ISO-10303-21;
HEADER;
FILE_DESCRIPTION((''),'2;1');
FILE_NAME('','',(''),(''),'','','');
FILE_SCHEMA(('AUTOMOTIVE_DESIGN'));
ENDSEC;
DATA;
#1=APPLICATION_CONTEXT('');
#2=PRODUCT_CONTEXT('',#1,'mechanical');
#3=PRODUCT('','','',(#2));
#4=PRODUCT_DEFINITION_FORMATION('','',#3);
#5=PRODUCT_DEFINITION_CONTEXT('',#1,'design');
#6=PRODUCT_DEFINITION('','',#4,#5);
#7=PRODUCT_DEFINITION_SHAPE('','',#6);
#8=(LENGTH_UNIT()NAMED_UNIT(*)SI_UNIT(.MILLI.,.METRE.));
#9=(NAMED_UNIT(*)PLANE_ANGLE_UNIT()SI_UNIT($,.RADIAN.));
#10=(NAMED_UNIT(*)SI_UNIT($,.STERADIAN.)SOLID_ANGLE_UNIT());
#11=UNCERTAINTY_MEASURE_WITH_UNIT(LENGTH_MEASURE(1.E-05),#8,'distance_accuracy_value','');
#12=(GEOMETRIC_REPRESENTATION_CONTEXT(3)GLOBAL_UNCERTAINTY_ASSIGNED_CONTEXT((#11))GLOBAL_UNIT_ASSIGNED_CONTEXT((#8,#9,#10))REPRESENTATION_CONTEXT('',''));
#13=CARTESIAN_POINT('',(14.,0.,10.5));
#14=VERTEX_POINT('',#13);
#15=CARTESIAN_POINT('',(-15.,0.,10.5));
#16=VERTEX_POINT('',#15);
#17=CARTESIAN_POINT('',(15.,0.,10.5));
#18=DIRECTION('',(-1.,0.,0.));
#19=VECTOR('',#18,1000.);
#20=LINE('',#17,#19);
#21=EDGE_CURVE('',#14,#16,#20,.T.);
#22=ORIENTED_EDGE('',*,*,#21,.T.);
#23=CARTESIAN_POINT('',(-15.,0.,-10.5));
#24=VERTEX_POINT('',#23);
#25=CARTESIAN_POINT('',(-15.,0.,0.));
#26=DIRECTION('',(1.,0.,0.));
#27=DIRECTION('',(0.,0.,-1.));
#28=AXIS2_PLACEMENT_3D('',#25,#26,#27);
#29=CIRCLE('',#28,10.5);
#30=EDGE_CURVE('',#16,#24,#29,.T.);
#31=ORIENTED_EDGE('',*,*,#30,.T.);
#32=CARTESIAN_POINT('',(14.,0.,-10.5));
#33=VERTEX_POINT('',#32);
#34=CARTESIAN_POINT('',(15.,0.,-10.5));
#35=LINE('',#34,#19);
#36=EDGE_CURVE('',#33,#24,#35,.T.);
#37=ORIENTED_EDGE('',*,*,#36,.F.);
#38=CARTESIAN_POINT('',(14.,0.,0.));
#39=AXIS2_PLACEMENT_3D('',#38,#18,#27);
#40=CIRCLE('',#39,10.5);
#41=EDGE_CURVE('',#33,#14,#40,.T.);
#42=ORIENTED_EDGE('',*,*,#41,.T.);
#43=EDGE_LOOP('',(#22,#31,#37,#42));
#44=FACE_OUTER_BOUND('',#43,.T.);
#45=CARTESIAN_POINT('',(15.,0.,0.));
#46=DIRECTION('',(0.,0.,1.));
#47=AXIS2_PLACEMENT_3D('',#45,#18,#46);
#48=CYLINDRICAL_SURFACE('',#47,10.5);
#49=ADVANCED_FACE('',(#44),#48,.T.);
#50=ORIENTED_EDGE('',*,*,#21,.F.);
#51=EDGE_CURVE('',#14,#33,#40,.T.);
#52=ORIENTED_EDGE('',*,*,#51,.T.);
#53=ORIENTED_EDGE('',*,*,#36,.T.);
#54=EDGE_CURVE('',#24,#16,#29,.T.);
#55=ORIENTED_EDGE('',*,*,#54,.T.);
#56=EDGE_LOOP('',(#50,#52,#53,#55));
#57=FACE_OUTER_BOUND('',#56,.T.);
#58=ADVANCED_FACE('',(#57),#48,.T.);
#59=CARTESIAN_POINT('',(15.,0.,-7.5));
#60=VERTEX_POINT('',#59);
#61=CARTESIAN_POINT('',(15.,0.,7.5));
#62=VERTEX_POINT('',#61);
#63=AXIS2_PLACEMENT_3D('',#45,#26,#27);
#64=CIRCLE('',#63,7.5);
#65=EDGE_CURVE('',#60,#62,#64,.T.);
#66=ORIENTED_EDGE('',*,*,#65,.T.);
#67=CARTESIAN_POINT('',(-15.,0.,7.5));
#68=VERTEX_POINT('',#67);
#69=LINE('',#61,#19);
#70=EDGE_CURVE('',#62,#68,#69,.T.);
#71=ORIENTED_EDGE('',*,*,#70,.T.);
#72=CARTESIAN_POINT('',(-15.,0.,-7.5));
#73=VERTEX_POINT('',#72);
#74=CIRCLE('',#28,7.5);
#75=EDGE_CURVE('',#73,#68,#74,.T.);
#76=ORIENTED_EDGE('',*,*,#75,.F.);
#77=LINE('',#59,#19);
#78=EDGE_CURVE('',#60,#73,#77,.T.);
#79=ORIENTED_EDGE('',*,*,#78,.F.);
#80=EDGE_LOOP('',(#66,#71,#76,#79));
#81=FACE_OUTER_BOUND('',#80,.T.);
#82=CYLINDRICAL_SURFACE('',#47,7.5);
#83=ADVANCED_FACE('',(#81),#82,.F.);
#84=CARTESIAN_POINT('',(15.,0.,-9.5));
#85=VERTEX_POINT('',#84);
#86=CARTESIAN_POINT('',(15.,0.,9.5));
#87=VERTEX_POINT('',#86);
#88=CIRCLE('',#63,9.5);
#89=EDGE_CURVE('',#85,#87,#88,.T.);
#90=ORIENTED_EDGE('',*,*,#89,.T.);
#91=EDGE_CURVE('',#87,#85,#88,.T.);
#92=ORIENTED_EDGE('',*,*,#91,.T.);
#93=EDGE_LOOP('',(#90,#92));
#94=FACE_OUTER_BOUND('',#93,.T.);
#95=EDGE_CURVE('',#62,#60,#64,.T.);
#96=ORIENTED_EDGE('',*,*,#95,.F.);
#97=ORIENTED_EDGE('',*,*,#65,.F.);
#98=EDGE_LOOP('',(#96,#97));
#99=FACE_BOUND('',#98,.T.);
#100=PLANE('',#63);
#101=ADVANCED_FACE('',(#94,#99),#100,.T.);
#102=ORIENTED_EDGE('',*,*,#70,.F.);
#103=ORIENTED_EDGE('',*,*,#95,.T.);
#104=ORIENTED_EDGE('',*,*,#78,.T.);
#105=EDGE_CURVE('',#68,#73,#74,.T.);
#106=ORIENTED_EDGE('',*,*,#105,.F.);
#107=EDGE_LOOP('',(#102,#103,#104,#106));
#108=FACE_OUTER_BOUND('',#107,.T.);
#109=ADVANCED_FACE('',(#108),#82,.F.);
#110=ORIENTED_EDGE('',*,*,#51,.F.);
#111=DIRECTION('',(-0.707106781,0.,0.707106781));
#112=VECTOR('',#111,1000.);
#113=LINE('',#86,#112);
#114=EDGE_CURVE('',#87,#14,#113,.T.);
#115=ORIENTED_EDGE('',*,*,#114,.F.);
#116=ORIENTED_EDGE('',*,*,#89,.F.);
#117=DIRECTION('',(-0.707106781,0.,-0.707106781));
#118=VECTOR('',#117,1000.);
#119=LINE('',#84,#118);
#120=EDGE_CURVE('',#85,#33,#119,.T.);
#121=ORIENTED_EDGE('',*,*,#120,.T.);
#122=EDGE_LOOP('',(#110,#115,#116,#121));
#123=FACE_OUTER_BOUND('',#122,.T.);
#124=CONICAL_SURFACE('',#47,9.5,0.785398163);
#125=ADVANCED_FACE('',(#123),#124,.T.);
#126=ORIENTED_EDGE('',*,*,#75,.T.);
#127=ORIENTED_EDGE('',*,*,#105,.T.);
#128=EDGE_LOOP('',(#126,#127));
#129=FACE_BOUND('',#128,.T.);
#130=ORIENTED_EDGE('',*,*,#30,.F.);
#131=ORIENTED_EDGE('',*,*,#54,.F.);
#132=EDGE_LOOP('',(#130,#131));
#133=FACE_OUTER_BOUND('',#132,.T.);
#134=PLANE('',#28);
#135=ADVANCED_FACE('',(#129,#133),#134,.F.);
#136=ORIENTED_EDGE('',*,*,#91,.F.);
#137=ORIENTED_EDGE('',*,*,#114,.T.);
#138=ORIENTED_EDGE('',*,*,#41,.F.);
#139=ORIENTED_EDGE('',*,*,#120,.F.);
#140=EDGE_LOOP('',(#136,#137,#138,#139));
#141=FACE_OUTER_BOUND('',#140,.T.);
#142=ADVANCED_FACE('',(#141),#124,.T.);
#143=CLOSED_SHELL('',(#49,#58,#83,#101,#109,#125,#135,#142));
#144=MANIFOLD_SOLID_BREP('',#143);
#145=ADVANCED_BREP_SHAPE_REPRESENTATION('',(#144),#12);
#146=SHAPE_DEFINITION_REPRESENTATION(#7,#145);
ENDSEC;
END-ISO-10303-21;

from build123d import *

# Parameters (mm, degrees)
SKETCH_1_R      = 10.5
SKETCH_1_R_2    = 7.5
EXTRUDE_1_DEPTH = 15
CHAMFER_1_SIZE  = 1


with BuildPart() as part:
    # 草图1 → 凸台-拉伸1 (new, symmetric)
    with BuildSketch(Plane(origin=(0, 0, 0), x_dir=(0, 0, -1), z_dir=(1, 0, 0))):
        Circle(SKETCH_1_R)
        Circle(SKETCH_1_R_2, mode=Mode.SUBTRACT)
    extrude(amount=EXTRUDE_1_DEPTH, both=True)

    # 倒角1
    chamfer_1_edges = [part.edges().sort_by_distance(p)[0] for p in [
        (15, 0, 10.5),
    ]]
    chamfer(chamfer_1_edges, length=CHAMFER_1_SIZE)


solid = part.part
